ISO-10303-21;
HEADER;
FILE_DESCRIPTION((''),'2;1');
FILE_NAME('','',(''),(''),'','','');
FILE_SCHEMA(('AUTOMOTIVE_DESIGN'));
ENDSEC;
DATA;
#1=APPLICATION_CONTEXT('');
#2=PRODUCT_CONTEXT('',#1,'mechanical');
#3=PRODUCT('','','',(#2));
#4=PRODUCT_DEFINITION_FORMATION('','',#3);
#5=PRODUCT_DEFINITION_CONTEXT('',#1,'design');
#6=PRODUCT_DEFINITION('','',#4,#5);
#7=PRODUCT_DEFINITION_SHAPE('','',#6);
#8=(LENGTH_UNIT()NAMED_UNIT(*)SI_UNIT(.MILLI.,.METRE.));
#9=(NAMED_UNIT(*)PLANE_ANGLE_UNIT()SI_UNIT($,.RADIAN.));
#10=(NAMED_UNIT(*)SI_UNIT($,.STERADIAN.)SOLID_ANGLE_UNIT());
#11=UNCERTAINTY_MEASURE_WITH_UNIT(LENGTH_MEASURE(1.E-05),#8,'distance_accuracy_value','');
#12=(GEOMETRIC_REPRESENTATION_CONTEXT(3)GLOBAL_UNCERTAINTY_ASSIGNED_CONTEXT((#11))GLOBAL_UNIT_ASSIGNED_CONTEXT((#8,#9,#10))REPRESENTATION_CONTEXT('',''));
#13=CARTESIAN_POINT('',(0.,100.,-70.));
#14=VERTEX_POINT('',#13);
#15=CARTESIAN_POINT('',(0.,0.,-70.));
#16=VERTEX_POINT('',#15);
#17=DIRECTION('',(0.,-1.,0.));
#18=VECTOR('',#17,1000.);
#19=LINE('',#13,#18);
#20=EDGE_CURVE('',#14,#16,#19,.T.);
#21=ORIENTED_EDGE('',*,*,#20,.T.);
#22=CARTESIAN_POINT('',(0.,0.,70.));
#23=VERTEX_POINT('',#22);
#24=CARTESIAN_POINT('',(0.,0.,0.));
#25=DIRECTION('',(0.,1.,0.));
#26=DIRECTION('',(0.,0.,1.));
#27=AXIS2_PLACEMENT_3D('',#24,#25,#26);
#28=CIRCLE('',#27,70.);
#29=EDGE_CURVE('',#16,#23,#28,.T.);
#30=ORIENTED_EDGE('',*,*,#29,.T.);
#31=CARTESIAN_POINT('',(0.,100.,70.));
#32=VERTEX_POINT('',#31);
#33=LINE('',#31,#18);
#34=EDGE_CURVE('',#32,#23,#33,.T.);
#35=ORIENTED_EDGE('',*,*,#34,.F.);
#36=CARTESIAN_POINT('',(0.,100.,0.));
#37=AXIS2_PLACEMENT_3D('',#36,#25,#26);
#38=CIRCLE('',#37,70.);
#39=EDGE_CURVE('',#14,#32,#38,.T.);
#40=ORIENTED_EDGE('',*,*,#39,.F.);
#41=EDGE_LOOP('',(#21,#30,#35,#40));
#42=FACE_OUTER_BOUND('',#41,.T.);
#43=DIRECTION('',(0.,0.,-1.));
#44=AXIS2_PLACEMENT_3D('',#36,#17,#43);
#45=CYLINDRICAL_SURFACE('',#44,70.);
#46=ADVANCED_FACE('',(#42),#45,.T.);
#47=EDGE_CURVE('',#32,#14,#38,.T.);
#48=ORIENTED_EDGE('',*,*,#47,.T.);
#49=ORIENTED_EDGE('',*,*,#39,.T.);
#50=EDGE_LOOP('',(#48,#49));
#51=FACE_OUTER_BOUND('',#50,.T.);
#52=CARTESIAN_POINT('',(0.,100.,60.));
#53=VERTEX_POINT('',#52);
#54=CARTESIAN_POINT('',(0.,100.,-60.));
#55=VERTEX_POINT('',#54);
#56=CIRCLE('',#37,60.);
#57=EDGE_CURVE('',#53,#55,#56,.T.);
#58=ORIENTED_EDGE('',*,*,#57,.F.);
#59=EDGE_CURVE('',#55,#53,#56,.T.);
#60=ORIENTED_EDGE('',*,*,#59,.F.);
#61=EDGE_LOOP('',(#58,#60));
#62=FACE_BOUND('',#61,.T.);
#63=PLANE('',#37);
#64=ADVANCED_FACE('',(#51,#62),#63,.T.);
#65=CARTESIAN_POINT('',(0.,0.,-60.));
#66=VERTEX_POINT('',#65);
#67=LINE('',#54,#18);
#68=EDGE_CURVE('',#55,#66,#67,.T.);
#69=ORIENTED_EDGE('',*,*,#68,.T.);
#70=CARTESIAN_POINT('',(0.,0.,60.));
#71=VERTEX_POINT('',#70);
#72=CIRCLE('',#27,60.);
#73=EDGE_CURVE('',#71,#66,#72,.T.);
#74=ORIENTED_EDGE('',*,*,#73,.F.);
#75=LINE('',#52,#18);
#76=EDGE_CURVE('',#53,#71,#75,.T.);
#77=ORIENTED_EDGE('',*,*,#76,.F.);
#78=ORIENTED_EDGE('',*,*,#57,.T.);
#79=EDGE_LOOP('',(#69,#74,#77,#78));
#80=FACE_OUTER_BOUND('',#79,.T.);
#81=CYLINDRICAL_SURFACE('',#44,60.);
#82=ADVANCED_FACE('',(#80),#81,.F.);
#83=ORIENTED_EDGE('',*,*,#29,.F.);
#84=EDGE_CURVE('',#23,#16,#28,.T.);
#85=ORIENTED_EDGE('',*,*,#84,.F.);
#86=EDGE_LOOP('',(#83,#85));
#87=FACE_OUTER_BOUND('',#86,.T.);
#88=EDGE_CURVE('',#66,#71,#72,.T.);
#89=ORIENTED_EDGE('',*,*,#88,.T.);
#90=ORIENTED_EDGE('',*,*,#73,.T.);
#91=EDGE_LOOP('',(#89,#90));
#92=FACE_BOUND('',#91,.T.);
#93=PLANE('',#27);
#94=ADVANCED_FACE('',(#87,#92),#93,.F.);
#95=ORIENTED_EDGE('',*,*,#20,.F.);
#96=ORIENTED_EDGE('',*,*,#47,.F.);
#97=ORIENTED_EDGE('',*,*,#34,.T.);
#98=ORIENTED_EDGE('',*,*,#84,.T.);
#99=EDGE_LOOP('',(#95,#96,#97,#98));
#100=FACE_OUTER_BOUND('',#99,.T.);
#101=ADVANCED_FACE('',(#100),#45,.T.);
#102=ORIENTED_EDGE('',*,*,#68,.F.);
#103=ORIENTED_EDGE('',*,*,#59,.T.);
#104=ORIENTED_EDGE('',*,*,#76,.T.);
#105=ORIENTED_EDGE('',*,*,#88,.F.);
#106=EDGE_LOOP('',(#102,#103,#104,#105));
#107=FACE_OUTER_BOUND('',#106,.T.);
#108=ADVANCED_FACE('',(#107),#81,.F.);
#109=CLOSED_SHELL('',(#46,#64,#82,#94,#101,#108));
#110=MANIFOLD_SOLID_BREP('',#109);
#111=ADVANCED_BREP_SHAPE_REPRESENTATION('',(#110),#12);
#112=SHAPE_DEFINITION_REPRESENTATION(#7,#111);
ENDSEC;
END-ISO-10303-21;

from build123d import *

# Parameters (mm, degrees)
SKETCH1_R           = 70
SKETCH1_R_2         = 60
BOSS_EXTRUDE1_DEPTH = 100


with BuildPart() as part:
    # Sketch1 → Boss-Extrude1 (new body)
    with BuildSketch(Plane(origin=(0, 0, 0), x_dir=(1, 0, 0), z_dir=(0, 1, 0))):
        with Locations(Location((0, 0, 0), (0, 0, 270))):
            Circle(SKETCH1_R)
        with Locations(Location((0, 0, 0), (0, 0, 270))):
            Circle(SKETCH1_R_2, mode=Mode.SUBTRACT)
    extrude(amount=BOSS_EXTRUDE1_DEPTH)


solid = part.part
